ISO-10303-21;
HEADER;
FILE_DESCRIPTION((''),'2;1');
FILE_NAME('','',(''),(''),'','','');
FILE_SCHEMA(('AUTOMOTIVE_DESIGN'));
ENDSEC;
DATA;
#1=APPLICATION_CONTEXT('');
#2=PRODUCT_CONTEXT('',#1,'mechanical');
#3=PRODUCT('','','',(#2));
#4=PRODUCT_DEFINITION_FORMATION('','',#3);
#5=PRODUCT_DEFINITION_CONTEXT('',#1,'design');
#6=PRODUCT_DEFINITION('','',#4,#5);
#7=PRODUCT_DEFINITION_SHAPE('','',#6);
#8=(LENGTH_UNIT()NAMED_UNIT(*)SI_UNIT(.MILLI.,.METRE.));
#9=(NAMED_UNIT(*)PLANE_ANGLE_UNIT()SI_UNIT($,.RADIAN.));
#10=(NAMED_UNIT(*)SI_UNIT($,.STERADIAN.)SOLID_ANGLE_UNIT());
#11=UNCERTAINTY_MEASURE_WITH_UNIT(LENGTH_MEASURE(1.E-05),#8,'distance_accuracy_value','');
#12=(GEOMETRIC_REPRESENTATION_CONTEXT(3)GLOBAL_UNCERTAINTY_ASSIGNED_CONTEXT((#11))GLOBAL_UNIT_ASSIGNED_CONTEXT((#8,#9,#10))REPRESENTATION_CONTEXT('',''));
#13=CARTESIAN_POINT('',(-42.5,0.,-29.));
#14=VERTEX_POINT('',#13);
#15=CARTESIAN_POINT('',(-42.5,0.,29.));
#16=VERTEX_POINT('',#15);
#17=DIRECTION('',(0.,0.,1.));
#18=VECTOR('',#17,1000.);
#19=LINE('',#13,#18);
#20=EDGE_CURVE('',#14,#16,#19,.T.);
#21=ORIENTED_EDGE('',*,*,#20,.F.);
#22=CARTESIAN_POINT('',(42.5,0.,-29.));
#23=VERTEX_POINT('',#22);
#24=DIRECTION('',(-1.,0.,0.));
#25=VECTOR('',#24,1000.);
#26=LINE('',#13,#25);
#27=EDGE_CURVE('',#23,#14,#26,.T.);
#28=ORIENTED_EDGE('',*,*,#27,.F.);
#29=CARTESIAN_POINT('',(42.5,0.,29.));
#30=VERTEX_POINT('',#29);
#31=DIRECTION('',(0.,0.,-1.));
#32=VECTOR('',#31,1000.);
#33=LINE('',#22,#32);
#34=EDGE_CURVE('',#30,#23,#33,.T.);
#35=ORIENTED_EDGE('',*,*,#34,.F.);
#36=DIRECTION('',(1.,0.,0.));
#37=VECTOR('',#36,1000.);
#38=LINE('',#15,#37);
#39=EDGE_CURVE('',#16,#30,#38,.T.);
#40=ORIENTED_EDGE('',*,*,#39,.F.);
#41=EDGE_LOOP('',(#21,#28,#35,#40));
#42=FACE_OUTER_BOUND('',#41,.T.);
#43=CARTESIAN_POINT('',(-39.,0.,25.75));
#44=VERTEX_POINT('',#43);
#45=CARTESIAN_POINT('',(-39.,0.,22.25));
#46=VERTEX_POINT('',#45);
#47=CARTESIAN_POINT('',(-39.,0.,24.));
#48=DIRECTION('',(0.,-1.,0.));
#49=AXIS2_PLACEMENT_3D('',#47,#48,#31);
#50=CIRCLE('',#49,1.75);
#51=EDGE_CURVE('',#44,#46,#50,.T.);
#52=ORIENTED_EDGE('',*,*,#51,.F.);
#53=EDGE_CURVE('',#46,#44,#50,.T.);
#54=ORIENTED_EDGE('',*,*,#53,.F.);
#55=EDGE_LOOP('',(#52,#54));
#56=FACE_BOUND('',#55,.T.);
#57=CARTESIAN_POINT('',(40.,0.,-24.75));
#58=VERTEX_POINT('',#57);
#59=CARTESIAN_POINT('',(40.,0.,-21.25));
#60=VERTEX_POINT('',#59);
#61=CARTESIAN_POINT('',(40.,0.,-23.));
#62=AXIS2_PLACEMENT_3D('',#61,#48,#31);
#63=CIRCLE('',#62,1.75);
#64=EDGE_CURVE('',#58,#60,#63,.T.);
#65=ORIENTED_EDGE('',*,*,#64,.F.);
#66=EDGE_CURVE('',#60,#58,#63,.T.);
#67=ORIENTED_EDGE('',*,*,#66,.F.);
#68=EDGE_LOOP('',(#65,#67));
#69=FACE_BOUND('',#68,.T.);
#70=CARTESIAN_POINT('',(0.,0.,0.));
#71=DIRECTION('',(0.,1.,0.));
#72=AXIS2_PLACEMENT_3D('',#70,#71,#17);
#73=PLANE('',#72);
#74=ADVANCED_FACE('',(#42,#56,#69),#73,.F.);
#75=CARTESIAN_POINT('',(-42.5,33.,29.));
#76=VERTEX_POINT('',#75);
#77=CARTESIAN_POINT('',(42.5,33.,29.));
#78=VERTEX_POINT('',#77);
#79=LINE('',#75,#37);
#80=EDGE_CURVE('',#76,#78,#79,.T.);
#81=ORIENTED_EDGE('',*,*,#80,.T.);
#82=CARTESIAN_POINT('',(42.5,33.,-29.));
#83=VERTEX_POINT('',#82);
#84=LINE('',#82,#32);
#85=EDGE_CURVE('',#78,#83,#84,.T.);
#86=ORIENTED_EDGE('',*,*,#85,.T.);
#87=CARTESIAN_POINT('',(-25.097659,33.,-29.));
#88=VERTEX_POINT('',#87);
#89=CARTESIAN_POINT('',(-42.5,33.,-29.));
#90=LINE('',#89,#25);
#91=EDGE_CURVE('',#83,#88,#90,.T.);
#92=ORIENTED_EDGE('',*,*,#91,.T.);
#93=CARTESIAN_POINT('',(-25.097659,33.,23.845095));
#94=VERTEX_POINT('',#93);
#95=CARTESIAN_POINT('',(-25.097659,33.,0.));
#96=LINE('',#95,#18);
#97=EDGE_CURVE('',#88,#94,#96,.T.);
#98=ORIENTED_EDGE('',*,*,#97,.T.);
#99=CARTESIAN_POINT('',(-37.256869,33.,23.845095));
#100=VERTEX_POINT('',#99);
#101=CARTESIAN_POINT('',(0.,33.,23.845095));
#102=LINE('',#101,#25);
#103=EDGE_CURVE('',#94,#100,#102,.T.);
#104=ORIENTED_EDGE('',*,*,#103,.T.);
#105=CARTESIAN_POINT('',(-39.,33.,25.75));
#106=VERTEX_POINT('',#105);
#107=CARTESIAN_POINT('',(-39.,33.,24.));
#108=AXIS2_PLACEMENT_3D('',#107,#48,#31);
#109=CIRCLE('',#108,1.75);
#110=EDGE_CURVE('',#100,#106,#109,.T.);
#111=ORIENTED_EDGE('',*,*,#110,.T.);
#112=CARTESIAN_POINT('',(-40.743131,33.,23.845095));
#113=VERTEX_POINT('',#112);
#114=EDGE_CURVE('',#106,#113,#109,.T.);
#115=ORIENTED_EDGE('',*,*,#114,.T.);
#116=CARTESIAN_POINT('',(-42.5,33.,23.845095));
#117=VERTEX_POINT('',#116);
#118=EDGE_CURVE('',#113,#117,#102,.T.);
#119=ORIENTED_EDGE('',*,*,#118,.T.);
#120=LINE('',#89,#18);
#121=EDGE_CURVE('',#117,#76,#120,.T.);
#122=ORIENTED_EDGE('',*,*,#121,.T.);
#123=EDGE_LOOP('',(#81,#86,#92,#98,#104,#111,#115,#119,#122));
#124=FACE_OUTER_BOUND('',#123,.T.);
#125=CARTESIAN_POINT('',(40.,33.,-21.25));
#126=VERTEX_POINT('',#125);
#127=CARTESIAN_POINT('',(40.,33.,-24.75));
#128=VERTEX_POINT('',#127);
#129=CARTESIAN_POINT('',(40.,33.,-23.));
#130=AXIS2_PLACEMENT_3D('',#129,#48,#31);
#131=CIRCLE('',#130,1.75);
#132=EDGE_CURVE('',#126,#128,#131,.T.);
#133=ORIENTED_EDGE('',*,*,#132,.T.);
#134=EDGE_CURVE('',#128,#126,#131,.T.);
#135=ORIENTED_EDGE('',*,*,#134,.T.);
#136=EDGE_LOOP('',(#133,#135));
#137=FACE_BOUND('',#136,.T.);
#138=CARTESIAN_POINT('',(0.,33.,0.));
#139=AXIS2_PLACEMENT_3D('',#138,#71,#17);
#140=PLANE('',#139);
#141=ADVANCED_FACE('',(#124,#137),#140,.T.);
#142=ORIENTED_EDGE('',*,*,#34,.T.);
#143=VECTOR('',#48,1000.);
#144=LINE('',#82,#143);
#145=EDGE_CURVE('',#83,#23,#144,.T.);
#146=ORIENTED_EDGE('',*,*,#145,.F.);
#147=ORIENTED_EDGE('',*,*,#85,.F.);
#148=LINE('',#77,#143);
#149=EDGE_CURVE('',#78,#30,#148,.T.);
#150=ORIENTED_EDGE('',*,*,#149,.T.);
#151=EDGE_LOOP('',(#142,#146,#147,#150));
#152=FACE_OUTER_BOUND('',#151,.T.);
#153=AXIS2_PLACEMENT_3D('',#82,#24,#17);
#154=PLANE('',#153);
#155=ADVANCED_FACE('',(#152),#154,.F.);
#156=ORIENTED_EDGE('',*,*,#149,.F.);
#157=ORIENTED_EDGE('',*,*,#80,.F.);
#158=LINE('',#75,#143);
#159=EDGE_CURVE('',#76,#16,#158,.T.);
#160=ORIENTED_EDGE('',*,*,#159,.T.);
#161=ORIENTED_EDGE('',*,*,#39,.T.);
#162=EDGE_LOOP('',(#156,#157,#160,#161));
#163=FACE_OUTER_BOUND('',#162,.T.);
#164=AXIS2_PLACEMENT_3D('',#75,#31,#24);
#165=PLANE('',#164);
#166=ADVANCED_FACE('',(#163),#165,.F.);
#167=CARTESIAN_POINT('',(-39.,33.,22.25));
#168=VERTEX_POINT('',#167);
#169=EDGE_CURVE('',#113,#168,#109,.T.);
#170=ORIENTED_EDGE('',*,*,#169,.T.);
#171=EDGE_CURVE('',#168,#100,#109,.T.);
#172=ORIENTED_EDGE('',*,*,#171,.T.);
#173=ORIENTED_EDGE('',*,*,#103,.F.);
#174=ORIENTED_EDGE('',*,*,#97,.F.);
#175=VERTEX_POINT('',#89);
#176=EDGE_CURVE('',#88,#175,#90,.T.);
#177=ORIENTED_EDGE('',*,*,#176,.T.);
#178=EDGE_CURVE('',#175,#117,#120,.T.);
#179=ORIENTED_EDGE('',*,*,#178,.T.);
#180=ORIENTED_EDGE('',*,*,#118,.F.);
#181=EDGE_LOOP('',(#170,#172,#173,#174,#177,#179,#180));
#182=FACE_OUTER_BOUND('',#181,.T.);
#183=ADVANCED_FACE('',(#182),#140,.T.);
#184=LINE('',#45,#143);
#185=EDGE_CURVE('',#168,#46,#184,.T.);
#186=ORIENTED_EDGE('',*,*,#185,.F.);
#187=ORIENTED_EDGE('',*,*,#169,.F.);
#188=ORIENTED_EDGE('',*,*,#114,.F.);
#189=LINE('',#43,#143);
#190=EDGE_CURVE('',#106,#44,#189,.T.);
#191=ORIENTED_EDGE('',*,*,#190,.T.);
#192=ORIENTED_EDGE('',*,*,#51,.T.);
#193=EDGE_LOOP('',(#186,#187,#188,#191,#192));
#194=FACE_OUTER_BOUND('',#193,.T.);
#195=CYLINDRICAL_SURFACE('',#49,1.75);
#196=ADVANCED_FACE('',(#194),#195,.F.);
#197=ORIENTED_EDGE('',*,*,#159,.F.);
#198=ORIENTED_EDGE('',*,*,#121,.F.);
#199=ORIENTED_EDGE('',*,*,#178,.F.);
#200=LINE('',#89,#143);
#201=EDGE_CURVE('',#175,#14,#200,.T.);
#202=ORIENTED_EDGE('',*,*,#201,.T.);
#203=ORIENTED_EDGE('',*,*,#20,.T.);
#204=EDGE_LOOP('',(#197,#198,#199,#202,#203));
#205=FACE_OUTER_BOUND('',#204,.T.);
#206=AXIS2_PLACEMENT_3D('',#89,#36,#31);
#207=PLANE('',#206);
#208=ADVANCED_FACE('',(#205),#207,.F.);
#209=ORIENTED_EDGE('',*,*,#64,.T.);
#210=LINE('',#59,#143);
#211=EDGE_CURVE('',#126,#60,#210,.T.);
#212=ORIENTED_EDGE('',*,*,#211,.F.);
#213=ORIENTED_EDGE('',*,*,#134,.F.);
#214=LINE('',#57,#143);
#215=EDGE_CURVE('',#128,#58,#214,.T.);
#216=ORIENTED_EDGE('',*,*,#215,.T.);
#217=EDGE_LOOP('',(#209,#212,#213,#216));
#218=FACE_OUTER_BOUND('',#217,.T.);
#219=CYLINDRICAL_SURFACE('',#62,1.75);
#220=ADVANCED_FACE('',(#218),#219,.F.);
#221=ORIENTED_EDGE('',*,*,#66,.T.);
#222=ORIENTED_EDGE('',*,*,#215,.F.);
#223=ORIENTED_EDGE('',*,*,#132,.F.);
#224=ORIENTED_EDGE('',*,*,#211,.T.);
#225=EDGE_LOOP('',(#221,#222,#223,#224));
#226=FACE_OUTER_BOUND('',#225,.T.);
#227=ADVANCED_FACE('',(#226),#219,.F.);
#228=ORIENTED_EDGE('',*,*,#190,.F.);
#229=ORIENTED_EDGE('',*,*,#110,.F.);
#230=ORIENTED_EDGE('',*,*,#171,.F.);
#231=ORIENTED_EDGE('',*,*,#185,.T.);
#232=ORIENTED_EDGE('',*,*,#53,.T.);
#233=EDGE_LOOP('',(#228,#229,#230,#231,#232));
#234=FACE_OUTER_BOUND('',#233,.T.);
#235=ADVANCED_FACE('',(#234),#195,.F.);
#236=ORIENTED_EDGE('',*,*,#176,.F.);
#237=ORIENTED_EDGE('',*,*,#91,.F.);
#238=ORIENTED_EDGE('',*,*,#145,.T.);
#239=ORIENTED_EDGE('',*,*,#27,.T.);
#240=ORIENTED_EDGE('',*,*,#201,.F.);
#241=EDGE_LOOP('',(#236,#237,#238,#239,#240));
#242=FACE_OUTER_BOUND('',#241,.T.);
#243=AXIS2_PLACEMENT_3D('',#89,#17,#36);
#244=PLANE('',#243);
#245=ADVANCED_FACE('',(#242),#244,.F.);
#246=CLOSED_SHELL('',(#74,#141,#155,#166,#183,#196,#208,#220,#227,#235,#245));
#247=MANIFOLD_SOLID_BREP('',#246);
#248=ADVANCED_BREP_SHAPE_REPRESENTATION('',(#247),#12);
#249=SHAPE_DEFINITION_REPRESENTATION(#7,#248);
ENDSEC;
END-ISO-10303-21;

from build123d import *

# Parameters (mm, degrees)
SKETCH_1_W              = 85
SKETCH_1_H              = 58
EXTRUDE_1_DEPTH         = 33
HOLE_WIZARD_3_5_3_5_1_D = 3.5


with BuildPart() as part:
    # 草图1 → 凸台-拉伸1 (new body)
    with BuildSketch(Plane(origin=(0, 0, 0), x_dir=(1, 0, 0), z_dir=(0, 1, 0))):
        Rectangle(SKETCH_1_W, SKETCH_1_H)
    extrude(amount=EXTRUDE_1_DEPTH)

    # Ø3.5 (3.5) 直径孔1 (through all)
    with Locations(Plane(origin=(0, 0, 0), x_dir=(-1, 0, 0), z_dir=(0, -1, 0))):
        with Locations((39, -24), (-40, 23)):
            Hole(HOLE_WIZARD_3_5_3_5_1_D / 2)


solid = part.part
